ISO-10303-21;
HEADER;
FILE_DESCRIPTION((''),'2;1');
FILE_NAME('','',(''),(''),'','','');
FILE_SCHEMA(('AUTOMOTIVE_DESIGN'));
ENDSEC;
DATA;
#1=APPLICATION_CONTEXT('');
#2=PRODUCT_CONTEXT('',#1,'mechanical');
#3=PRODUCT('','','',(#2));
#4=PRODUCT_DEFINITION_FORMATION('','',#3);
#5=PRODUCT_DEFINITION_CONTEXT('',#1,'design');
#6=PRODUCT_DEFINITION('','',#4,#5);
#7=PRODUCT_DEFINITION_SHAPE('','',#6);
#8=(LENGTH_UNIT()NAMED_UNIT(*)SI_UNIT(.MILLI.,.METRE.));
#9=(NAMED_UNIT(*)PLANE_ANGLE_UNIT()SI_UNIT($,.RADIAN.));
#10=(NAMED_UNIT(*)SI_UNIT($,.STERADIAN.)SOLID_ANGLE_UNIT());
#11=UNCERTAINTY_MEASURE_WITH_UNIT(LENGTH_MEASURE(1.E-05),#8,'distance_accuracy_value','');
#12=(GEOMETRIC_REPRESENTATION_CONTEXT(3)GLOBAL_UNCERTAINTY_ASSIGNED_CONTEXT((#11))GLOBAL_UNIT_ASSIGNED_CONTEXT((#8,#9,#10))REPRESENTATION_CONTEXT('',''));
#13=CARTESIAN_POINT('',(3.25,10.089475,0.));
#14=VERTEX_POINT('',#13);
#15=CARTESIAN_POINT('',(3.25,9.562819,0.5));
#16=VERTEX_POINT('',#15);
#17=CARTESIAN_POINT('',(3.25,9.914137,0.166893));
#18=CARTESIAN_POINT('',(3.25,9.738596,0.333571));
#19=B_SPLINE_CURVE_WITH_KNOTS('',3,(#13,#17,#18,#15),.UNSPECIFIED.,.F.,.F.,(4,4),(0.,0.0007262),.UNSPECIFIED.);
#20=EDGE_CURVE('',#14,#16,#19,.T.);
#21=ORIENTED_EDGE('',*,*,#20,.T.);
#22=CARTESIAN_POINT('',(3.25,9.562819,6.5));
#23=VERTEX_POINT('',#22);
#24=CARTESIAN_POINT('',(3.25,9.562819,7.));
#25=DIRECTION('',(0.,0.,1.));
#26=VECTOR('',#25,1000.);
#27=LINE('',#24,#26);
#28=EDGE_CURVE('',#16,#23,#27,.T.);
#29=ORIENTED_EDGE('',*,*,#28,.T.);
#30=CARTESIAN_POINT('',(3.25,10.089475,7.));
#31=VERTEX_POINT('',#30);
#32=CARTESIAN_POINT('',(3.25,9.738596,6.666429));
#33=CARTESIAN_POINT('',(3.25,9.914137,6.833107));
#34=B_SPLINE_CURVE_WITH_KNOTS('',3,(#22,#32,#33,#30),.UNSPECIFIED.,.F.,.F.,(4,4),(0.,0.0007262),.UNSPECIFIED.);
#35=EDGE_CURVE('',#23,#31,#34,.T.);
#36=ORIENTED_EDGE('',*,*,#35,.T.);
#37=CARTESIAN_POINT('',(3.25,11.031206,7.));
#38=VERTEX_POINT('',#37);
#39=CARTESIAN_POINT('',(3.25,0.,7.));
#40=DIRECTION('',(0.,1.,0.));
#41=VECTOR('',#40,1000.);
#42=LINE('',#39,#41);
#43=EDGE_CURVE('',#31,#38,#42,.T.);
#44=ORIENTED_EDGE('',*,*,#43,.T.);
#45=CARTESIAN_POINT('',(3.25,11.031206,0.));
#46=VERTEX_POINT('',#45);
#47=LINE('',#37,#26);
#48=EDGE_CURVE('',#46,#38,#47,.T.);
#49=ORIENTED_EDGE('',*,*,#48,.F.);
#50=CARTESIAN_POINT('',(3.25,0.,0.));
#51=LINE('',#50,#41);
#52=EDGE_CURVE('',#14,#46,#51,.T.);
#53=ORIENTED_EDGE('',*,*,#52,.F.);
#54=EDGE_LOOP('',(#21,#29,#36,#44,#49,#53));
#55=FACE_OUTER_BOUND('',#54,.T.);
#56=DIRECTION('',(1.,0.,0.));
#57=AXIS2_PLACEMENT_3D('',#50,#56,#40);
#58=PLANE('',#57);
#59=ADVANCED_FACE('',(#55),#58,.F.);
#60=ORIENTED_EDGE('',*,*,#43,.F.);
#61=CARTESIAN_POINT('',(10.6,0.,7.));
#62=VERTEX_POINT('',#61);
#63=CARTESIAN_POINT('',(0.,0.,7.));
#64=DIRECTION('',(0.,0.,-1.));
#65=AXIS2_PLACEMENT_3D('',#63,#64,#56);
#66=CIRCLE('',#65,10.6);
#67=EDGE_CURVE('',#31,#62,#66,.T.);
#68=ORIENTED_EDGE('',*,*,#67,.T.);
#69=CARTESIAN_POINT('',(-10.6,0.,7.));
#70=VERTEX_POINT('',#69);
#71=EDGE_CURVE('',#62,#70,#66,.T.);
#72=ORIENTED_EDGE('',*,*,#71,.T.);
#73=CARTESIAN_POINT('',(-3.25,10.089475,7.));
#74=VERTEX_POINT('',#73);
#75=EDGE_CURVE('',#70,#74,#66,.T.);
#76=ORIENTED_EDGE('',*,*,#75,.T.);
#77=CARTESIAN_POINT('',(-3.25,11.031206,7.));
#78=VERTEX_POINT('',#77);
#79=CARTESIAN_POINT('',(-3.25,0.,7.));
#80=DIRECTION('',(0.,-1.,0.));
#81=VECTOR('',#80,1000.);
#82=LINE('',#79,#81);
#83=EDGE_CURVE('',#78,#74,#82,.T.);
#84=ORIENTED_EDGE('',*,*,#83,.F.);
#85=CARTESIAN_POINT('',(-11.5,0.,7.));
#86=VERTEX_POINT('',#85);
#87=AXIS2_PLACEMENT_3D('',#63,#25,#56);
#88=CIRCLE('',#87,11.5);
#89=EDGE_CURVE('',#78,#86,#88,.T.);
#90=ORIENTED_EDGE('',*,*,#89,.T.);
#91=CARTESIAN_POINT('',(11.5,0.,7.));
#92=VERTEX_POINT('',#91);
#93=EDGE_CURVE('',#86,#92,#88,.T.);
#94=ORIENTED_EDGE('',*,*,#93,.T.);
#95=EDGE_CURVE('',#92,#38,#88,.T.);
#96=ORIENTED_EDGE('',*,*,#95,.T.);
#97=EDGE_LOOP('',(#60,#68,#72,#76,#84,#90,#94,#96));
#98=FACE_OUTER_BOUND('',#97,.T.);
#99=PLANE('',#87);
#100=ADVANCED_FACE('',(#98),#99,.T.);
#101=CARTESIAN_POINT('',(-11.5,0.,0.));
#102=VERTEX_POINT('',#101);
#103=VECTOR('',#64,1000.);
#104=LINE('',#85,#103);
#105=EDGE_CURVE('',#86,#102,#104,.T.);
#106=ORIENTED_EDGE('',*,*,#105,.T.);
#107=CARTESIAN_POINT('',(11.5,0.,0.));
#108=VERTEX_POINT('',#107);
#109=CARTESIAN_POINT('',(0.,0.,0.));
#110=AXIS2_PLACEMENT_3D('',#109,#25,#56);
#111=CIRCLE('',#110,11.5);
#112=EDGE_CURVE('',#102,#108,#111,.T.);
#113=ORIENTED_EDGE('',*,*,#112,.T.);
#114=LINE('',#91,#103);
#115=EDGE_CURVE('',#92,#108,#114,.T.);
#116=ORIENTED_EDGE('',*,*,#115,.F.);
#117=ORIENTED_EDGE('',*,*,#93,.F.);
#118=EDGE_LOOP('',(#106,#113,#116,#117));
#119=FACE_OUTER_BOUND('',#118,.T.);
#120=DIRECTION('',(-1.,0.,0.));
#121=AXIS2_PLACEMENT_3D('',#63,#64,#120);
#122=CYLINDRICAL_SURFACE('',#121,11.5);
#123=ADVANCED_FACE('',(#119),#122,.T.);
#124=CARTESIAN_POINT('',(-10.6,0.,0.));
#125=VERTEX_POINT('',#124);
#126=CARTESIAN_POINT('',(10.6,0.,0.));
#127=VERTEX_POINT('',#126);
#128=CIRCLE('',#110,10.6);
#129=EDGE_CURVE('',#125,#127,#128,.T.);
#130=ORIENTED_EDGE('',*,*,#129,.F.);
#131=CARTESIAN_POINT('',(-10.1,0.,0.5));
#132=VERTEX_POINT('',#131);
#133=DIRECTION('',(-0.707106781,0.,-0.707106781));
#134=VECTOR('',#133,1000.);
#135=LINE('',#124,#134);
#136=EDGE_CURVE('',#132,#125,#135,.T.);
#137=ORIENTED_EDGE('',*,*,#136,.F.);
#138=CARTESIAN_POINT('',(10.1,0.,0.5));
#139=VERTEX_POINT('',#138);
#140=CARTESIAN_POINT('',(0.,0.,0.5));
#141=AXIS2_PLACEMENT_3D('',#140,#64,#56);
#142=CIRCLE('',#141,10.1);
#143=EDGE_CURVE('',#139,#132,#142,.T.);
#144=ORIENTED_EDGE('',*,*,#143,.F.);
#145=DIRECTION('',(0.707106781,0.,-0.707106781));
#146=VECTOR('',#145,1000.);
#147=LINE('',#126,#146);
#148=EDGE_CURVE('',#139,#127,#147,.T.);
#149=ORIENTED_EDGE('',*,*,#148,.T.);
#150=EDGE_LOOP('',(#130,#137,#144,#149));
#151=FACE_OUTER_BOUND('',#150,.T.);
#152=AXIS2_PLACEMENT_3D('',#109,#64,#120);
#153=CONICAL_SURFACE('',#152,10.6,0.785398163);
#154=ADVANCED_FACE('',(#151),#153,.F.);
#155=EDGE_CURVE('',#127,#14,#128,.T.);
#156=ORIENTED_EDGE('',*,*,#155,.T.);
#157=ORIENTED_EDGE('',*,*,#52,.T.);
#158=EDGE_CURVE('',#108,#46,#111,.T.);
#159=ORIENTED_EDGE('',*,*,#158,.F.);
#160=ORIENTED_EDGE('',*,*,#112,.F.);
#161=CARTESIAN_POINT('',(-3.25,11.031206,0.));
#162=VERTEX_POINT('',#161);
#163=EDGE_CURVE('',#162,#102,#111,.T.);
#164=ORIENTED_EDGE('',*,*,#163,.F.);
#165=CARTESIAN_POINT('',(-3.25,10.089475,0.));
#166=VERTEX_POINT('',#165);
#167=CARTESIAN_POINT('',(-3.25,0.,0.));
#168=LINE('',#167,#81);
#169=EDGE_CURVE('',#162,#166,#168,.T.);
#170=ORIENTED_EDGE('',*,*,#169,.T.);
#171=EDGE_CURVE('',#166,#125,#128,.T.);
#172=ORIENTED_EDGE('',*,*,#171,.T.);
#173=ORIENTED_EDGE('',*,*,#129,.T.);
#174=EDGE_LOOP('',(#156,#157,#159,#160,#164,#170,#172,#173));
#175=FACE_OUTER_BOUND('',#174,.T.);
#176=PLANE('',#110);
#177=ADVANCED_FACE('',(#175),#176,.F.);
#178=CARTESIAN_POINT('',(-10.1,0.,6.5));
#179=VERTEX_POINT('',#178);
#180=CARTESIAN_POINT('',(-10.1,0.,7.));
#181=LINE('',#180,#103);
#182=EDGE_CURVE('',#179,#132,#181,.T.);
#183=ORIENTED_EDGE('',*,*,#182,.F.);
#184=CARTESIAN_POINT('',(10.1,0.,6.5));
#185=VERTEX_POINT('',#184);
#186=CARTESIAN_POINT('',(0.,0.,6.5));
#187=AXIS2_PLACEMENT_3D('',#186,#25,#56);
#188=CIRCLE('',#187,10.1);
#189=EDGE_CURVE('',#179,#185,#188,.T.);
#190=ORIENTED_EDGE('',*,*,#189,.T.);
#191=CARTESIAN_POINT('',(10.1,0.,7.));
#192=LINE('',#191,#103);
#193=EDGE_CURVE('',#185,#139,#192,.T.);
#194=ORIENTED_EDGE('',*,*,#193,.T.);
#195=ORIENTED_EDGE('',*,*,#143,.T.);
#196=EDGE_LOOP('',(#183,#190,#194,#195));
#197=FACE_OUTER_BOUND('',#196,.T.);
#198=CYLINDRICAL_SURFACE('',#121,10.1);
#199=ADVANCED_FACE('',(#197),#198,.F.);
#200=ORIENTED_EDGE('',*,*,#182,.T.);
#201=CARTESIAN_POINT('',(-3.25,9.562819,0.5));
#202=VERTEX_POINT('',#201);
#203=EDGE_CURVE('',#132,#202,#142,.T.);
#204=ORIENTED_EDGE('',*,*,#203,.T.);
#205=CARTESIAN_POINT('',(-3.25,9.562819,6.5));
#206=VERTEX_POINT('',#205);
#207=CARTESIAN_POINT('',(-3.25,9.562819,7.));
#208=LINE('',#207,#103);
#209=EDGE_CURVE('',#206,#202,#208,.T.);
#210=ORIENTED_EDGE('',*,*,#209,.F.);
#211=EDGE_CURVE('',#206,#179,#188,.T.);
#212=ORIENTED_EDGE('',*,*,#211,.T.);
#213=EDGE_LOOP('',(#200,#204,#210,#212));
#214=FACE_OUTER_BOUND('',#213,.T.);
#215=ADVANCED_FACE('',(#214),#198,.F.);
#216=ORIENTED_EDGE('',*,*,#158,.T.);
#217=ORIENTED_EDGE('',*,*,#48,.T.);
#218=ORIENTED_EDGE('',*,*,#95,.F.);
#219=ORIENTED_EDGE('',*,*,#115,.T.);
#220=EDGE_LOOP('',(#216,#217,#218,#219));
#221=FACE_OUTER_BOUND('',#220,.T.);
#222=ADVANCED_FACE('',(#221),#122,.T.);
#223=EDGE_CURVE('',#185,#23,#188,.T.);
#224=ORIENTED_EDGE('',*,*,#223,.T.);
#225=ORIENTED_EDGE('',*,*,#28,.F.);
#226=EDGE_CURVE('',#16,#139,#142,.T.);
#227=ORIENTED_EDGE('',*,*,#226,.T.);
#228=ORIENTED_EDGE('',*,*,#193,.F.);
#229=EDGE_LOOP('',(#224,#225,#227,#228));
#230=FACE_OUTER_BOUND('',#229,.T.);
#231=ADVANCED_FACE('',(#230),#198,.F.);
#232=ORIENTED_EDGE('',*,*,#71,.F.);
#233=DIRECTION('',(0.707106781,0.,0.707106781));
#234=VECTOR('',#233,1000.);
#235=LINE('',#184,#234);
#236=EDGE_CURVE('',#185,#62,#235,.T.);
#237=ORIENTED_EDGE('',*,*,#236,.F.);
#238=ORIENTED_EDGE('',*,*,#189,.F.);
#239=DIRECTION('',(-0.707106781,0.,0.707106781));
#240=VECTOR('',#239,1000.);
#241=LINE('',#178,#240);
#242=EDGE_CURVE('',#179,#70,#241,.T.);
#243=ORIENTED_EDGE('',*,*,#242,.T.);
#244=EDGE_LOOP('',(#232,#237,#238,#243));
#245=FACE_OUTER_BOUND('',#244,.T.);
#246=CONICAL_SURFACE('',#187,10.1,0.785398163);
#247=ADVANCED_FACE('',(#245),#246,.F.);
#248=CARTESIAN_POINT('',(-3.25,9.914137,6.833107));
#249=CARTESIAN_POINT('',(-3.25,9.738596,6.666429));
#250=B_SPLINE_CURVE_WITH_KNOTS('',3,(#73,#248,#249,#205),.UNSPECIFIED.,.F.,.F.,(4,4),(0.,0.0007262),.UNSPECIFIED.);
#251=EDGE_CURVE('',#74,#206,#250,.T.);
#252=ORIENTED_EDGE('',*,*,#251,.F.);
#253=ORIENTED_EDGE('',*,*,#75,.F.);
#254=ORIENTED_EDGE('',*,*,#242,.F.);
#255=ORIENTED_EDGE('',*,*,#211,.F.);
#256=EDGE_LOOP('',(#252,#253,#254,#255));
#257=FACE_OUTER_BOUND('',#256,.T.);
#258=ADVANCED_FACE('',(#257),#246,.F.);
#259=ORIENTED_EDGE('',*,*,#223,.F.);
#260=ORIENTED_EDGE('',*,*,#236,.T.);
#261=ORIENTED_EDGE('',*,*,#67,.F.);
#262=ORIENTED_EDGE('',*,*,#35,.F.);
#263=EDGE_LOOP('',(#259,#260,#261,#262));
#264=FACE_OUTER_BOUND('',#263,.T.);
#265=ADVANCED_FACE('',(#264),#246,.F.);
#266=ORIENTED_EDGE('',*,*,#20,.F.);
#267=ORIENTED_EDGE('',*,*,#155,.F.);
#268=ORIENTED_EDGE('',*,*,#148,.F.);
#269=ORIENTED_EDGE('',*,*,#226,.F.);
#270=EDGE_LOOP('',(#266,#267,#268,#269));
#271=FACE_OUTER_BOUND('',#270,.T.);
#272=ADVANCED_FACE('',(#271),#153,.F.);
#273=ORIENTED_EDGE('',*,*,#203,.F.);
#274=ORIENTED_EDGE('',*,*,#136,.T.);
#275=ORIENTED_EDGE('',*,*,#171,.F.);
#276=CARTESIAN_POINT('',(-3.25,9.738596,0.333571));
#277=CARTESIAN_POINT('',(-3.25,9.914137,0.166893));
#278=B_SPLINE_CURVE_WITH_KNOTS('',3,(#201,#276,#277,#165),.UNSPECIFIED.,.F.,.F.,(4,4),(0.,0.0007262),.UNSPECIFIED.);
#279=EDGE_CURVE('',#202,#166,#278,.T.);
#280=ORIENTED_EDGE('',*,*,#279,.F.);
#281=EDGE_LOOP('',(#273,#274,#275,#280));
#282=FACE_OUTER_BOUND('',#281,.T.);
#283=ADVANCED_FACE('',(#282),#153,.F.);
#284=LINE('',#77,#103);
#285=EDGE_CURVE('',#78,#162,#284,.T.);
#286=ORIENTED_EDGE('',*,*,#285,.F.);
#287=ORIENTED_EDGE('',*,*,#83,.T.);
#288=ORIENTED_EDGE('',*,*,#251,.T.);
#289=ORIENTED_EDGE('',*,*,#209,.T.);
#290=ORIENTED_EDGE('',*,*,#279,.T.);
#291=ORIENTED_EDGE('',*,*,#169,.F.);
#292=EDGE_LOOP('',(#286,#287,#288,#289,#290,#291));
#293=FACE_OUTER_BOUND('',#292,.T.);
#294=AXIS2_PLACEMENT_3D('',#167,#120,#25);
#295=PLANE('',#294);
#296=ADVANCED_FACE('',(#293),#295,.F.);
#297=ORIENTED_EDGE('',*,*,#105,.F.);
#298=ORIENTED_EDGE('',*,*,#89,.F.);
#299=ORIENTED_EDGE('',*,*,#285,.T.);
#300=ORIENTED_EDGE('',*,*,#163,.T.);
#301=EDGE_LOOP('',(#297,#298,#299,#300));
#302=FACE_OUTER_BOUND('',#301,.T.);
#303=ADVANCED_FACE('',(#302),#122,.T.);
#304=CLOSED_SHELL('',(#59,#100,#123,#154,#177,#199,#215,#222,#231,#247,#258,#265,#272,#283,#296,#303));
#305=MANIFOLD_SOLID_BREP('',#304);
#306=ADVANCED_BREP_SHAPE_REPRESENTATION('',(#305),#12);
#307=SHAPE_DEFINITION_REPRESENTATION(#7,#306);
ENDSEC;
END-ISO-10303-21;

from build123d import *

# Parameters (mm, degrees)
SKETCH1_R           = 11.5
SKETCH1_R_2         = 10.1
BOSS_EXTRUDE1_DEPTH = 7
SKETCH2_W           = 6.5
SKETCH2_H           = 15
CUT_EXTRUDE1_DEPTH  = 18.70593121
CHAMFER1_SIZE       = 0.5


with BuildPart() as part:
    # Sketch1 → Boss-Extrude1 (new body)
    with BuildSketch(Plane.XY):
        Circle(SKETCH1_R)
        Circle(SKETCH1_R_2, mode=Mode.SUBTRACT)
    extrude(amount=BOSS_EXTRUDE1_DEPTH)

    # Sketch2 → Cut-Extrude1 (cut, through all)
    with BuildSketch(Plane.XY.offset(7)):
        with Locations((0, 7.5)):
            Rectangle(SKETCH2_W, SKETCH2_H)
    extrude(amount=-CUT_EXTRUDE1_DEPTH, mode=Mode.SUBTRACT)

    # Chamfer1
    chamfer1_edges = [part.edges().sort_by_distance(p)[0] for p in [
        (0, -10.1, 0),
        (0, -10.1, 7),
    ]]
    chamfer(chamfer1_edges, length=CHAMFER1_SIZE)


solid = part.part
